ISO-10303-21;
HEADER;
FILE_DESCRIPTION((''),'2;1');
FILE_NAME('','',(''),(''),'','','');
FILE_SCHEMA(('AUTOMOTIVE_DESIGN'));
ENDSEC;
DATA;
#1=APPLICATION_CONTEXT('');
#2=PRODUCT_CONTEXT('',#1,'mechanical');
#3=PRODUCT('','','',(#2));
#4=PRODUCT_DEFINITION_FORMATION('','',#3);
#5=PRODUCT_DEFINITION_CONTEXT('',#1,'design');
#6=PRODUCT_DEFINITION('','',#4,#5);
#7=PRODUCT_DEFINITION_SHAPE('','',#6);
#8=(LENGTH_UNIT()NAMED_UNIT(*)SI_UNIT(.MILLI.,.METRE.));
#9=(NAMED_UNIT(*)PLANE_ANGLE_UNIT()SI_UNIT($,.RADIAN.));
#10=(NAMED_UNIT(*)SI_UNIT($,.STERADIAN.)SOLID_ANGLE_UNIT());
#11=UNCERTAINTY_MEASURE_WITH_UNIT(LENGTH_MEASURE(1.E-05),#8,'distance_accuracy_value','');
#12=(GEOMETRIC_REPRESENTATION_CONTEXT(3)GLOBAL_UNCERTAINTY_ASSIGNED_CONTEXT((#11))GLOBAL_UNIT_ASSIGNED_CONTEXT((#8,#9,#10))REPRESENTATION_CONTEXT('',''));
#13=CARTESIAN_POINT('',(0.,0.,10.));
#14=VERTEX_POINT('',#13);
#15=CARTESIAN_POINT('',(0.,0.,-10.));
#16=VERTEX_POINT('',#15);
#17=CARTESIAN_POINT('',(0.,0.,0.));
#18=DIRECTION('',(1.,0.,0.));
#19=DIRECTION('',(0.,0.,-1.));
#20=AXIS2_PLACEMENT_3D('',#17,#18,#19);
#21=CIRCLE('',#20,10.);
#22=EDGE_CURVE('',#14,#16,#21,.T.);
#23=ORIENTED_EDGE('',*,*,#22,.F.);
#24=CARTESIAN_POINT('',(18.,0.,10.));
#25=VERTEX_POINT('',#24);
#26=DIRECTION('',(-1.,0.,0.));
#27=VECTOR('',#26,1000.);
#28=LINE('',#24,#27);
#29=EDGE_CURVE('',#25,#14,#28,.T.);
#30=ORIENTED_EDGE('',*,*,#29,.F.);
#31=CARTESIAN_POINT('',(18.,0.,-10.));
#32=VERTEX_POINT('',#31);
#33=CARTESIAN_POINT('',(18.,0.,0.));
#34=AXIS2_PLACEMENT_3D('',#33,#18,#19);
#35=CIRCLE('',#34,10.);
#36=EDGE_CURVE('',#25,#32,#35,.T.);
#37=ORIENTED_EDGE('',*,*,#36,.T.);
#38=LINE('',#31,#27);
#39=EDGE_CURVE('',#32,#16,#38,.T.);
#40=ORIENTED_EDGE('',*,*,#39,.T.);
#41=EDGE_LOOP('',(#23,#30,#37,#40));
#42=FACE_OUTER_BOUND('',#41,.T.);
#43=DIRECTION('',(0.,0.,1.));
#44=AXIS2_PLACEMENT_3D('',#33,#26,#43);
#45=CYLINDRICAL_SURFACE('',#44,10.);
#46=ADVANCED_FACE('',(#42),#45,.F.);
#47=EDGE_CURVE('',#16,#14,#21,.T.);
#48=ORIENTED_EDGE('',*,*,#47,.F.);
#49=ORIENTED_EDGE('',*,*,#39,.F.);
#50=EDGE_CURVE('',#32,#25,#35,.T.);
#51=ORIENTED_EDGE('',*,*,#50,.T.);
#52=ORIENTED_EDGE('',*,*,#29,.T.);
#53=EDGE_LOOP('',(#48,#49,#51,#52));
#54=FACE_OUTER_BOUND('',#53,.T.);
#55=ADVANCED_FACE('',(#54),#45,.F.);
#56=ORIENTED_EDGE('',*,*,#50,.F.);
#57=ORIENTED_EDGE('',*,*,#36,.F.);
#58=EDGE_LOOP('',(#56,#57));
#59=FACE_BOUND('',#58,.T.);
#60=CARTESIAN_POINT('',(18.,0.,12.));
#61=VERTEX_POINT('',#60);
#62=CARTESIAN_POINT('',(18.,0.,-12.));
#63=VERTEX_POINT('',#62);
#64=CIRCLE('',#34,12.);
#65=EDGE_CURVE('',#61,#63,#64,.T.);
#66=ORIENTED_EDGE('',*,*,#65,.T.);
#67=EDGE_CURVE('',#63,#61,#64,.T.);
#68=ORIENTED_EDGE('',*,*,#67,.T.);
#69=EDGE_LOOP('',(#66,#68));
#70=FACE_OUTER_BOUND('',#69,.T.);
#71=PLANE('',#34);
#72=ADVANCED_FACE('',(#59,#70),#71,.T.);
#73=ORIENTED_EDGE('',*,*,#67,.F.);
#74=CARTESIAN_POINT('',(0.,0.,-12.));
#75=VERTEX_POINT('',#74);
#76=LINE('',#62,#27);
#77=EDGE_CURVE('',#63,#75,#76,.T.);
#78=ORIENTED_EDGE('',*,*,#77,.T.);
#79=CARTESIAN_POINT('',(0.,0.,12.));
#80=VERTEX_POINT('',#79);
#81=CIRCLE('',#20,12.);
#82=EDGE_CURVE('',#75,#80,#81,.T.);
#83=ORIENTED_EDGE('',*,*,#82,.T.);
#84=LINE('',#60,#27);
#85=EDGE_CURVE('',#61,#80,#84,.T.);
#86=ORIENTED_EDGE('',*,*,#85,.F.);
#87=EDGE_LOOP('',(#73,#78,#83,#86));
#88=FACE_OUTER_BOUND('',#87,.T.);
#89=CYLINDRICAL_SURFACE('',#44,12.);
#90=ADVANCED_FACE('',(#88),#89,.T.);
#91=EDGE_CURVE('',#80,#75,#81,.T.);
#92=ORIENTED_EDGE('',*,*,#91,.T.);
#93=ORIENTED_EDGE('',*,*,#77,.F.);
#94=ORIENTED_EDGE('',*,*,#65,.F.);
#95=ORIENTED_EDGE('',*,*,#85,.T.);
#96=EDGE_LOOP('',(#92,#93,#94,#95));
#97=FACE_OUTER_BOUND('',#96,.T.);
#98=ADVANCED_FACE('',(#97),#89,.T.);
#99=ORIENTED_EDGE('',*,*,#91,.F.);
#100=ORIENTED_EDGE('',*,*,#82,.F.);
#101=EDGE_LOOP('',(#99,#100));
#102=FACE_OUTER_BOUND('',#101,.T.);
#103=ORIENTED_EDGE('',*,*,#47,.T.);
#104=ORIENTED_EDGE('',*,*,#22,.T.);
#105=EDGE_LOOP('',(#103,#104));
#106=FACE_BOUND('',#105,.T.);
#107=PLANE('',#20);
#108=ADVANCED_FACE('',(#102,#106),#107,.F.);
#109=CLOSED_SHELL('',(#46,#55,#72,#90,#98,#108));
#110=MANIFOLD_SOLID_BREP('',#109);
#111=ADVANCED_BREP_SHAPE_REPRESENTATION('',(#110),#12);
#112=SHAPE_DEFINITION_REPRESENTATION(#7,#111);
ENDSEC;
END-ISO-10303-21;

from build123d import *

# Parameters (mm, degrees)
SKETCH1_R           = 12
SKETCH1_R_2         = 10
BOSS_EXTRUDE1_DEPTH = 18


with BuildPart() as part:
    # Sketch1 → Boss-Extrude1 (new body)
    with BuildSketch(Plane(origin=(0, 0, 0), x_dir=(0, 0, -1), z_dir=(1, 0, 0))):
        Circle(SKETCH1_R)
        Circle(SKETCH1_R_2, mode=Mode.SUBTRACT)
    extrude(amount=BOSS_EXTRUDE1_DEPTH)


solid = part.part
